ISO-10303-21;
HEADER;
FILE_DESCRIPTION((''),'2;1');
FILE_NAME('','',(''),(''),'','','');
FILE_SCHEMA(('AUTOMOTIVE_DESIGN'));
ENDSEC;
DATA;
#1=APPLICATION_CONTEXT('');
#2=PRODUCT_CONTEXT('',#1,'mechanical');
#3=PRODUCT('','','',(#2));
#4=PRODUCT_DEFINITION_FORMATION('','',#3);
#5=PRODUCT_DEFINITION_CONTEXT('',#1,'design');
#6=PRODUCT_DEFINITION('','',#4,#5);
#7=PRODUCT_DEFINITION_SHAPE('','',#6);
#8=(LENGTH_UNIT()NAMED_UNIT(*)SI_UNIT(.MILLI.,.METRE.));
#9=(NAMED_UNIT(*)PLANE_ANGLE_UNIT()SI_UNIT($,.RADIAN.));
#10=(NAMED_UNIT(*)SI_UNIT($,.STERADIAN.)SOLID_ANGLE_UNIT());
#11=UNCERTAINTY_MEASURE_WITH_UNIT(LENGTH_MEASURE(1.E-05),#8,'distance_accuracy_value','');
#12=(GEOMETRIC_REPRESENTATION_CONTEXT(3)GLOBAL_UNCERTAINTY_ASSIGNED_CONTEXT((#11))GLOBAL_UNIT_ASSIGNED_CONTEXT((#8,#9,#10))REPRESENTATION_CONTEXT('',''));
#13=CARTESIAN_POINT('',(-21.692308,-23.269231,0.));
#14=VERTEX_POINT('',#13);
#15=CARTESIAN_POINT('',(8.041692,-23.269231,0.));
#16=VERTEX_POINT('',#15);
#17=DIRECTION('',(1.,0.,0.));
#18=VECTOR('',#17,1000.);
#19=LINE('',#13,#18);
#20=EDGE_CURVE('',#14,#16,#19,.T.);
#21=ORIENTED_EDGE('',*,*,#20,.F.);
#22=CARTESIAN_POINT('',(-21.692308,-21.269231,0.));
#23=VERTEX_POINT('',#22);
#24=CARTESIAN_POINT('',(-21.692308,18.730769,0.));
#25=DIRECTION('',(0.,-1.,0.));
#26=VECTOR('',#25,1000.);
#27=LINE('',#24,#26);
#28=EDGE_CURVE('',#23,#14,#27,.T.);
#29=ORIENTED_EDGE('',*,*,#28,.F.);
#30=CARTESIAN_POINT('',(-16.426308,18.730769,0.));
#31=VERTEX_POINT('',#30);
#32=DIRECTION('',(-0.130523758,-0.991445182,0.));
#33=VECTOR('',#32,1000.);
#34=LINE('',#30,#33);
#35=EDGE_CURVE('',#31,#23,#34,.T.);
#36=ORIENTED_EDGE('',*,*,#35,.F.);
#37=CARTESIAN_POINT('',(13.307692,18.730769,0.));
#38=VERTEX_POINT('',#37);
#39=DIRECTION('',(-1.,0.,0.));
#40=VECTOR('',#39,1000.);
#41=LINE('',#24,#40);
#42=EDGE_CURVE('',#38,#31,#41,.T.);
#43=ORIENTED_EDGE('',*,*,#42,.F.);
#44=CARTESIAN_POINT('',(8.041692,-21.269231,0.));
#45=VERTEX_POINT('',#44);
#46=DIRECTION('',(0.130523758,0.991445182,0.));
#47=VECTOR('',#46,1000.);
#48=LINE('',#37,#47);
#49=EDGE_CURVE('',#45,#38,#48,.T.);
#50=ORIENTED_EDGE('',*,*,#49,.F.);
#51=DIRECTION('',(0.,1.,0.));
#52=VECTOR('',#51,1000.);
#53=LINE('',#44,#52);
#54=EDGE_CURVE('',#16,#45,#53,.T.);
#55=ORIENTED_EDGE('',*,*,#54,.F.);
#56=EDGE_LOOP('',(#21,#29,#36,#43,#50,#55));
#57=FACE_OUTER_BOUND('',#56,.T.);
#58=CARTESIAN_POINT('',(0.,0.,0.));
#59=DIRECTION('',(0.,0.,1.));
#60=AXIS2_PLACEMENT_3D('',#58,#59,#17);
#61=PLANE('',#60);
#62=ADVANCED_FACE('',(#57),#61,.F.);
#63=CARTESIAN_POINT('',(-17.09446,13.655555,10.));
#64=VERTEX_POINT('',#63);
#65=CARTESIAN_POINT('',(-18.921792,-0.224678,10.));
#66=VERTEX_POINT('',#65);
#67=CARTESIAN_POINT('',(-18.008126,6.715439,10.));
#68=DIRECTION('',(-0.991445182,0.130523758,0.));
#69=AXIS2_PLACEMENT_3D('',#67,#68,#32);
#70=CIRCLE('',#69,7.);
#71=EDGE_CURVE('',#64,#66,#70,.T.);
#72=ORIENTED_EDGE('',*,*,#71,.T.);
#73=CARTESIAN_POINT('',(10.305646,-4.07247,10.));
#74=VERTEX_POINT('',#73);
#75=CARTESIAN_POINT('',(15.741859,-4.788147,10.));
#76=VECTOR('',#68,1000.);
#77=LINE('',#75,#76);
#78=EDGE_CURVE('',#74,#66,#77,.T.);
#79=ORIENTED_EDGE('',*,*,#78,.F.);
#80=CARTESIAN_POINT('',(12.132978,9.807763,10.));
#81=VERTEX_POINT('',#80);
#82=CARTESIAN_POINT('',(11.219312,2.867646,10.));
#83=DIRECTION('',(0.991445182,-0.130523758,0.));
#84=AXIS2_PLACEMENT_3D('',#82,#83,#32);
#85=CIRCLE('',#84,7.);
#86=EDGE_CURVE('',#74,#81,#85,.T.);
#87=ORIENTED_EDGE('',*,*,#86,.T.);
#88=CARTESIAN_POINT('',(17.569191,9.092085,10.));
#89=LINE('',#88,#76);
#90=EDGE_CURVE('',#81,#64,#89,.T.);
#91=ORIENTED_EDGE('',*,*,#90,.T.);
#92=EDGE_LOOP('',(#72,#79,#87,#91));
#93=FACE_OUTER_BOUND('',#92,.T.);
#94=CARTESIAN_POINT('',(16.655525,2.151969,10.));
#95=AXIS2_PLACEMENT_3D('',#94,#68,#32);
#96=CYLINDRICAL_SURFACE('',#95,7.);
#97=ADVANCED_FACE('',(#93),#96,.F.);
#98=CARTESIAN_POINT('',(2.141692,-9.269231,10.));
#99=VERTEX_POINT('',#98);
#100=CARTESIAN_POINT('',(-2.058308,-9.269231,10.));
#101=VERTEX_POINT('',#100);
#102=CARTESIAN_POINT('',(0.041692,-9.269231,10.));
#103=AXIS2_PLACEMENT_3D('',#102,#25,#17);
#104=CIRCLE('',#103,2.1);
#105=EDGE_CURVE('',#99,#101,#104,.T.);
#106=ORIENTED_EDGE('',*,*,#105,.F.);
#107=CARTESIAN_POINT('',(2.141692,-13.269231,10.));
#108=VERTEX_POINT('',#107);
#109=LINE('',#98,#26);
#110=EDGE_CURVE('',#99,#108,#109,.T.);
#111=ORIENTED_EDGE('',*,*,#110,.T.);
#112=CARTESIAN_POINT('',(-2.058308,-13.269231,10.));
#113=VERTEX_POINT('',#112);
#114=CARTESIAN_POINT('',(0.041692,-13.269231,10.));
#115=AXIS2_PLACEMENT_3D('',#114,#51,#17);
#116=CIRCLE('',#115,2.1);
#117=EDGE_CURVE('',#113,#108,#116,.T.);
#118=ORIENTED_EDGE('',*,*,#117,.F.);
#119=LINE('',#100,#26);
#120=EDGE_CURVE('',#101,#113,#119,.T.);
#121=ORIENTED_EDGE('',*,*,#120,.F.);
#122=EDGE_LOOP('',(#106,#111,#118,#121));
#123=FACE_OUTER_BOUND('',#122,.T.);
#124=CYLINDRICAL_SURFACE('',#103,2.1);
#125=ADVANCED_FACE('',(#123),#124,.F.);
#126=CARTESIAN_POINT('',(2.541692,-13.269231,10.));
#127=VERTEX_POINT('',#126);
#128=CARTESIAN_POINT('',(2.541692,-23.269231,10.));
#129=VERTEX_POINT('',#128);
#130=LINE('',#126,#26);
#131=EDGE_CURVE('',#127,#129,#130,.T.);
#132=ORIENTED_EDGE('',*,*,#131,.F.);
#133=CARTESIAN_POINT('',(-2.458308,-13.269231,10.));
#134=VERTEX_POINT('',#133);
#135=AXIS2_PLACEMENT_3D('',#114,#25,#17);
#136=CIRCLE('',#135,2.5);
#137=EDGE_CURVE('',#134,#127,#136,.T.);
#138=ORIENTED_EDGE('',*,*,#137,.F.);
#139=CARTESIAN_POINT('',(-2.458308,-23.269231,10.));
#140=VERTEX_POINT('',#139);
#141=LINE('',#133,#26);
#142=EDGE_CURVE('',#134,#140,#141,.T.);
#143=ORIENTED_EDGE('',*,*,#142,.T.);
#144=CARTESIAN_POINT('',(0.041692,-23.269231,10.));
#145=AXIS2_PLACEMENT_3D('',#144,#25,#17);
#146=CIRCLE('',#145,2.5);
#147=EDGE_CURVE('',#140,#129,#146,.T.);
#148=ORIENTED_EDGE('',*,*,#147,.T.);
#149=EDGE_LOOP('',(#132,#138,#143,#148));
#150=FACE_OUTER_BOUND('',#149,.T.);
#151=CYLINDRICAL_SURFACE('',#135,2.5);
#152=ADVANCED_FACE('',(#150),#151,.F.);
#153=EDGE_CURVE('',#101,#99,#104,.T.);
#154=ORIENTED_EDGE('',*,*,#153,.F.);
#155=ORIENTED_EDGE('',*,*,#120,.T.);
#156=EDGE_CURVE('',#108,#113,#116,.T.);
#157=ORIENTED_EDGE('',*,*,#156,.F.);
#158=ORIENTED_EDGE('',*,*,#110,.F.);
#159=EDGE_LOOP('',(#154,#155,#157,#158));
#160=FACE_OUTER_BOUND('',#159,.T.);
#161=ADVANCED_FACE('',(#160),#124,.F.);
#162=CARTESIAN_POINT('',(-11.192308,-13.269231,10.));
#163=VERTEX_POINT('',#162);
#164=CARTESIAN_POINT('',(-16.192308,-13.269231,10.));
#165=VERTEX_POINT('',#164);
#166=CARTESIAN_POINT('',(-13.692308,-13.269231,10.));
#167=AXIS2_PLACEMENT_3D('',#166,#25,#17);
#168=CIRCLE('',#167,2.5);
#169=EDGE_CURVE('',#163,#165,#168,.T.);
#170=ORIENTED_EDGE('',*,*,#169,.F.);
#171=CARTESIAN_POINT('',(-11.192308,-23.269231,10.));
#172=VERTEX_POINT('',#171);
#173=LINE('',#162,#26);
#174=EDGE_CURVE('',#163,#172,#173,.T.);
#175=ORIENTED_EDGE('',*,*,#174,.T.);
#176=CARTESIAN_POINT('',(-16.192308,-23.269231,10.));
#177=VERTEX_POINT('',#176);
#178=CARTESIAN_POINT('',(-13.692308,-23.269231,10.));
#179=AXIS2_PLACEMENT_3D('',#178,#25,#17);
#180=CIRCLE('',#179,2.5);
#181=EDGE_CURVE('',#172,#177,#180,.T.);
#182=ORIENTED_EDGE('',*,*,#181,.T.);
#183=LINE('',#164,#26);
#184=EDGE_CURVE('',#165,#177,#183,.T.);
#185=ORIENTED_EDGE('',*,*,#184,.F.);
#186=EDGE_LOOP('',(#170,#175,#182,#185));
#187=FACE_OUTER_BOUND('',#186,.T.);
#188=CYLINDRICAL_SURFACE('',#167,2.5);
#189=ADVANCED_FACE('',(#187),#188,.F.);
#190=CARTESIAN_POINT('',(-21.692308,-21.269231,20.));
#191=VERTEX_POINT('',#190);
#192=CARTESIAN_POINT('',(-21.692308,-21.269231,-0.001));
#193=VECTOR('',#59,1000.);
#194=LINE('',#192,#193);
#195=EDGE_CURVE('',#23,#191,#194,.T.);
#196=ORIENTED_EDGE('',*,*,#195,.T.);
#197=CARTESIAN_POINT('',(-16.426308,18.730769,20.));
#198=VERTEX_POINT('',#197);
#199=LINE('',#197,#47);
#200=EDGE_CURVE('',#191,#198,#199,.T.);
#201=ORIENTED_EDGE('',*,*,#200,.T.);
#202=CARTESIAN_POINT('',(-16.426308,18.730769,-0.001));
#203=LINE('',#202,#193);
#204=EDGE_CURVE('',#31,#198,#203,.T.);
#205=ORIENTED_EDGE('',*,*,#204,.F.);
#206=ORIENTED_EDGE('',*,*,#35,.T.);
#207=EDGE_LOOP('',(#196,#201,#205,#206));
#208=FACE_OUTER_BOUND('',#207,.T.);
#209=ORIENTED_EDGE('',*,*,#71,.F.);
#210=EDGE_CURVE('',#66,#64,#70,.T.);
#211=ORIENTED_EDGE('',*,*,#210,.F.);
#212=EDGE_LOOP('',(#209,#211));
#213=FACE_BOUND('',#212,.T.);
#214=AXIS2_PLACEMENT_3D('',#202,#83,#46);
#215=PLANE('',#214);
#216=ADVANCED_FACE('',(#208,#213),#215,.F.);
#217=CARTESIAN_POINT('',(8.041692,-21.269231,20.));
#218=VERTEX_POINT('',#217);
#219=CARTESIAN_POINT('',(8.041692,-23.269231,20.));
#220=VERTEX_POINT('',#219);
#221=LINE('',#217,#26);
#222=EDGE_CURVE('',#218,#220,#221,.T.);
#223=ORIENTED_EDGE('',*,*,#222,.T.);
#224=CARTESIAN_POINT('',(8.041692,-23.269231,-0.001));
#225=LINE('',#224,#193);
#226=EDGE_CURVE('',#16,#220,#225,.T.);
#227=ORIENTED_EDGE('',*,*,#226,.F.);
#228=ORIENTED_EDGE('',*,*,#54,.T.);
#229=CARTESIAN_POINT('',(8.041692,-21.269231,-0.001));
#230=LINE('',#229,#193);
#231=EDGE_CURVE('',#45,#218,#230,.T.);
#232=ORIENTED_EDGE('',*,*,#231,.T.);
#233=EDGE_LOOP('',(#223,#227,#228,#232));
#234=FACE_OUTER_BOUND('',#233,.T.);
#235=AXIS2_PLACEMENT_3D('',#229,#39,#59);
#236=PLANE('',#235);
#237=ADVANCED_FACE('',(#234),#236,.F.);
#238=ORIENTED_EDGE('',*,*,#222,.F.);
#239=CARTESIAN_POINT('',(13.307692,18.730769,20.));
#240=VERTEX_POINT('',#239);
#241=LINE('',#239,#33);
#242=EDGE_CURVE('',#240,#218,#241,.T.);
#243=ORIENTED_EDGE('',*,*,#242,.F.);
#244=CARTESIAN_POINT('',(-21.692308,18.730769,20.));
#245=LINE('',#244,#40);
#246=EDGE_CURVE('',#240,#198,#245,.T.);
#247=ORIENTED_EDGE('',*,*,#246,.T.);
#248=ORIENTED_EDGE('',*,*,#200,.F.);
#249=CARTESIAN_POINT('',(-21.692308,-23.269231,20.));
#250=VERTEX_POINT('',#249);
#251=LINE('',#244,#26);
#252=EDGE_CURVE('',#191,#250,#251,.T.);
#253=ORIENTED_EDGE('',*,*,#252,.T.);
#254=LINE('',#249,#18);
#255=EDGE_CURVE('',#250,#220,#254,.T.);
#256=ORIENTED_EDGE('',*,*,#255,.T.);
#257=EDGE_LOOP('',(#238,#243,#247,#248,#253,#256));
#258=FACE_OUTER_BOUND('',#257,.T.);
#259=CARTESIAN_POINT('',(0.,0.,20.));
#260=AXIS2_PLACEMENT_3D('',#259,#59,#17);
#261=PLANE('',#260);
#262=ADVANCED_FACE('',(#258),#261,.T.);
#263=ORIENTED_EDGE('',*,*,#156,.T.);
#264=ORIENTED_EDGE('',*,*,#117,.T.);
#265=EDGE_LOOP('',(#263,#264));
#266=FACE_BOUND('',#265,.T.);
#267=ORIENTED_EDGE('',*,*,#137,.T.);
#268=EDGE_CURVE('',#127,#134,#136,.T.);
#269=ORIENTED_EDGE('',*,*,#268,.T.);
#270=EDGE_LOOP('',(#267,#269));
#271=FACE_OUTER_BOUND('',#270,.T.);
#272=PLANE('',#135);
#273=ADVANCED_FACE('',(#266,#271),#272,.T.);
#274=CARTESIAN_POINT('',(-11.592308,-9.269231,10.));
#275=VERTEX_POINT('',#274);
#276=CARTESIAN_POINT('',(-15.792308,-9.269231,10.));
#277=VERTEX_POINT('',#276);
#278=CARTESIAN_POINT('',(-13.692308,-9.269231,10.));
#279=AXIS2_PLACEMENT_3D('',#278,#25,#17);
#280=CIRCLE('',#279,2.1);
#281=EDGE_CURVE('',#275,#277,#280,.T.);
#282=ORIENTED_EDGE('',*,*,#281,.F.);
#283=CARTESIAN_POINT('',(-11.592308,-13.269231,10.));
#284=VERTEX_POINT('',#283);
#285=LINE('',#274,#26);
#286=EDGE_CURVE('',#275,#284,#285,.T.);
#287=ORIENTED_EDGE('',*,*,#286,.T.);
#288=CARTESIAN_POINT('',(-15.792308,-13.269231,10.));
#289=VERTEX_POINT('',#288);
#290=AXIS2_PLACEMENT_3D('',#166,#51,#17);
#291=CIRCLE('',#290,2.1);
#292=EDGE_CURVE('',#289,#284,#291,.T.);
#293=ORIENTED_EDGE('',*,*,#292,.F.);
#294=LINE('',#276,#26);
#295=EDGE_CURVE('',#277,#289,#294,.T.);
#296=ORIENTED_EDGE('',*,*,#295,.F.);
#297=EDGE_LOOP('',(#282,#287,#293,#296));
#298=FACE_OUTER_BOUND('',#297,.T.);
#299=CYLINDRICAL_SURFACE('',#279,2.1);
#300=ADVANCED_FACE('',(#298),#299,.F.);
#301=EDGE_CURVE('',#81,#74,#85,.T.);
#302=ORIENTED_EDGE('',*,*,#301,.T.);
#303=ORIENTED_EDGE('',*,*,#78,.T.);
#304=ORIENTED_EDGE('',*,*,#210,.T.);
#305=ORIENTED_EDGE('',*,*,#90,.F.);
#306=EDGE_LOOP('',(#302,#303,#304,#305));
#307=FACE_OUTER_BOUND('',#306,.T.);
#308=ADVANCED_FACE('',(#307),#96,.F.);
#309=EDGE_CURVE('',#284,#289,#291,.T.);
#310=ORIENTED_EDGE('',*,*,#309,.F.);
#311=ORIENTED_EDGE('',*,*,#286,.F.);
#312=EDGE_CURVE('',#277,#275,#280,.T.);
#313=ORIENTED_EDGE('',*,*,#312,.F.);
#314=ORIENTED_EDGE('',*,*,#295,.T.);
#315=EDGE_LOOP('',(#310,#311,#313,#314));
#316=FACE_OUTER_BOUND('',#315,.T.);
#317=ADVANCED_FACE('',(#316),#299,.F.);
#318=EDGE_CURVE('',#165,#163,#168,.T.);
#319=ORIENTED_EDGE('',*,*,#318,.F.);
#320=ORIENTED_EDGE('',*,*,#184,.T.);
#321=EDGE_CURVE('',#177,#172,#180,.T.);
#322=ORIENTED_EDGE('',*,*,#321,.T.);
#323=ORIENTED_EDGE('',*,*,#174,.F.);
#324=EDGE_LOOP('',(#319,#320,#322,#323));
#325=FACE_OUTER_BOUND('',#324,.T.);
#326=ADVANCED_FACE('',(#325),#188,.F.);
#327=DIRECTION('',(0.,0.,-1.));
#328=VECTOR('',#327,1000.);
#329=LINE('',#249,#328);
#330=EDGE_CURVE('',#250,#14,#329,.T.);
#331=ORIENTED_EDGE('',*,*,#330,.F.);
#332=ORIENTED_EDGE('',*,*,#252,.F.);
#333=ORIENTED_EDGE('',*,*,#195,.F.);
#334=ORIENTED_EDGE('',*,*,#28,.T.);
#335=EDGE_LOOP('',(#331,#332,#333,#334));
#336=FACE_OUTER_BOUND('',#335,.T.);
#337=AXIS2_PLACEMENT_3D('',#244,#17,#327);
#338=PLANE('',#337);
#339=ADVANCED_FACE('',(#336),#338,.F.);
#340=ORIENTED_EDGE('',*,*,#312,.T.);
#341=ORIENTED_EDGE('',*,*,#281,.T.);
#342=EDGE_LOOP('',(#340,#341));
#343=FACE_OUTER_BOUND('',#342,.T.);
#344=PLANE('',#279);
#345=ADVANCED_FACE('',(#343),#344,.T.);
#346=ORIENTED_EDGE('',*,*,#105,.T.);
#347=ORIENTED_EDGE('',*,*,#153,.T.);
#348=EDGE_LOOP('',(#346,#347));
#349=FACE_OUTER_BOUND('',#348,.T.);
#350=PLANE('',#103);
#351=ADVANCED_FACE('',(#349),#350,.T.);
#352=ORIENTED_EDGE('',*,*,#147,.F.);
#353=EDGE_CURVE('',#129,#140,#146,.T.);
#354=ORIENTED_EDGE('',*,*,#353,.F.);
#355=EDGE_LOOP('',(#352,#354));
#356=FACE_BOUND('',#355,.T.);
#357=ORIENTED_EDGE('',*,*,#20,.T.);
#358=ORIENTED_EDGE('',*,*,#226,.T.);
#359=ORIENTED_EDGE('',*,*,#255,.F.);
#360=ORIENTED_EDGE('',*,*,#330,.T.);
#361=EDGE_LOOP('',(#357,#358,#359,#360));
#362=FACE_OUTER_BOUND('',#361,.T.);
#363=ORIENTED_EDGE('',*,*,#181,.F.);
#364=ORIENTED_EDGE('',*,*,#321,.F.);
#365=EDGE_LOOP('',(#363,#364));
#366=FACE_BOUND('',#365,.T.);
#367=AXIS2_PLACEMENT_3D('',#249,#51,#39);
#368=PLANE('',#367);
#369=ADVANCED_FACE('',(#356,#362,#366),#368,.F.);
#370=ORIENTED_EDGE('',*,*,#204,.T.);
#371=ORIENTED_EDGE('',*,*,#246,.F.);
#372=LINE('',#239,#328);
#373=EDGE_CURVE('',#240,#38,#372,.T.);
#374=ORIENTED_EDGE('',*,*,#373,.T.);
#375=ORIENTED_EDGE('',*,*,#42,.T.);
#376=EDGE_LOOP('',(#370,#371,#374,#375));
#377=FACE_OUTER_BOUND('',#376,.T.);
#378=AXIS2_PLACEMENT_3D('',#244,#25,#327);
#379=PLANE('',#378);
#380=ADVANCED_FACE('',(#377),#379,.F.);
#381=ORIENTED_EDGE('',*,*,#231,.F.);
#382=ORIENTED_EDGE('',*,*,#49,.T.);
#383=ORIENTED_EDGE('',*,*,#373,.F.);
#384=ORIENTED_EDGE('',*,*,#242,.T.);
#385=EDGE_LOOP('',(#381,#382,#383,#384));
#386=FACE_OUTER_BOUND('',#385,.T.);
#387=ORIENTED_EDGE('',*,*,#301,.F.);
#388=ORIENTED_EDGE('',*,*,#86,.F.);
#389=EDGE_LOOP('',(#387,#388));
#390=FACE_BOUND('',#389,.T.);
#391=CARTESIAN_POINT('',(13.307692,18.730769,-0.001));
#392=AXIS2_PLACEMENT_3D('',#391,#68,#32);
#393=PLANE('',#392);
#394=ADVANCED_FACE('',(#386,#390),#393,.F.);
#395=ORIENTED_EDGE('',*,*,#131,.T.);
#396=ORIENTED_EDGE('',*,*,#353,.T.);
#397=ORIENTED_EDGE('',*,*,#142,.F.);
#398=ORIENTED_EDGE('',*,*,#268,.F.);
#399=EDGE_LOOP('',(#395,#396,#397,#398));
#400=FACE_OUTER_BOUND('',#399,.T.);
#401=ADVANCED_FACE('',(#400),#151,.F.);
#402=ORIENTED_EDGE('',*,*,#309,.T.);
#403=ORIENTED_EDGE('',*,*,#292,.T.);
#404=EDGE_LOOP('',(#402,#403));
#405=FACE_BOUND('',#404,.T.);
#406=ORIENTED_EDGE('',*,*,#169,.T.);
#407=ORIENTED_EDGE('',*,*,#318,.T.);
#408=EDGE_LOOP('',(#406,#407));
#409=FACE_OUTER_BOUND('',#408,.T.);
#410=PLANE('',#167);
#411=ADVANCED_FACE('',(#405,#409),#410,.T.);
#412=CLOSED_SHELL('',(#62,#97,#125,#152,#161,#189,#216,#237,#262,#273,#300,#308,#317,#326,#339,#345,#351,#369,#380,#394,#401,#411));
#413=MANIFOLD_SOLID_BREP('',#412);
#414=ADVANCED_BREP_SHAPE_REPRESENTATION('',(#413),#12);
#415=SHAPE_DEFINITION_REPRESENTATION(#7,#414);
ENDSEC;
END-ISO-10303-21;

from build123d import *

# Parameters (mm, degrees)
SKETCH_1_W          = 35
SKETCH_1_H          = 42
EXTRUDE_1_DEPTH     = 20
CUT_EXTRUDE_1_REACH = 39.577
CUT_EXTRUDE_2_REACH = 47.579
SKETCH_4_R          = 7
SKETCH_5_R          = 2.1
CUT_EXTRUDE_3_DEPTH = 14
SKETCH_6_R          = 2.5
CUT_EXTRUDE_4_DEPTH = 10


with BuildPart() as part:
    # 草图1 → 凸台-拉伸1 (new body)
    with BuildSketch(Plane.XY):
        with Locations((-4.192307692, -2.269230769)):
            Rectangle(SKETCH_1_W, SKETCH_1_H)
    extrude(amount=EXTRUDE_1_DEPTH)

    # 草图3 → 切除-拉伸1 (cut, up to next)
    with BuildSketch(Plane.XY.offset(20), mode=Mode.PRIVATE) as cut_extrude_1_sk1:
        Polygon((-21.692307692, 18.730769231), (-16.426307692, 18.730769231), (-21.692307692, -21.269230769), align=None)
    cut_extrude_1_tool1 = extrude(cut_extrude_1_sk1.sketch, amount=-CUT_EXTRUDE_1_REACH, mode=Mode.PRIVATE) & part.part
    # 草图3 → 切除-拉伸1 (cut, up to next)
    with BuildSketch(Plane.XY.offset(20), mode=Mode.PRIVATE) as cut_extrude_1_sk2:
        Polygon((13.307692308, 18.730769231), (8.041692308, -21.269230769), (8.041692308, -23.269230769), (13.307692308, -23.269230769), align=None)
    cut_extrude_1_tool2 = extrude(cut_extrude_1_sk2.sketch, amount=-CUT_EXTRUDE_1_REACH, mode=Mode.PRIVATE) & part.part
    add(cut_extrude_1_tool1.solids().sort_by_distance((-19.936974, 5.397436, 20))[0], mode=Mode.SUBTRACT)
    add(cut_extrude_1_tool2.solids().sort_by_distance((11.472571, -9.238928, 20))[0], mode=Mode.SUBTRACT)

    # 草图4 → 切除-拉伸2 (cut, up to next)
    with BuildSketch(Plane(origin=(-18.570357184, 2.444787523, 0), x_dir=(0, 0, 1), z_dir=(-0.9914451818173987, 0.13052375818626055, 0)), mode=Mode.PRIVATE) as cut_extrude_2_sk1:
        with Locations(Location((10, 4.307500918, 0), (0, 0, 270))):
            Circle(SKETCH_4_R)
    cut_extrude_2_tool1 = extrude(cut_extrude_2_sk1.sketch, amount=-CUT_EXTRUDE_2_REACH, mode=Mode.PRIVATE) & part.part
    add(cut_extrude_2_tool1.solids().sort_by_distance((-18.008126, 6.715439, 10))[0], mode=Mode.SUBTRACT)

    # 草图5 → 切除-拉伸3 (cut)
    with BuildSketch(Plane.XZ.offset(23.269230769)):
        with Locations((-13.692307692, 10)):
            Circle(SKETCH_5_R)
        with Locations((0.041692308, 10)):
            Circle(SKETCH_5_R)
    extrude(amount=-CUT_EXTRUDE_3_DEPTH, mode=Mode.SUBTRACT)

    # 草图6 → 切除-拉伸4 (cut)
    with BuildSketch(Plane.XZ.offset(23.269230769)):
        with Locations((-13.692307692, 10)):
            Circle(SKETCH_6_R)
        with Locations((0.041692308, 10)):
            Circle(SKETCH_6_R)
    extrude(amount=-CUT_EXTRUDE_4_DEPTH, mode=Mode.SUBTRACT)


solid = part.part
